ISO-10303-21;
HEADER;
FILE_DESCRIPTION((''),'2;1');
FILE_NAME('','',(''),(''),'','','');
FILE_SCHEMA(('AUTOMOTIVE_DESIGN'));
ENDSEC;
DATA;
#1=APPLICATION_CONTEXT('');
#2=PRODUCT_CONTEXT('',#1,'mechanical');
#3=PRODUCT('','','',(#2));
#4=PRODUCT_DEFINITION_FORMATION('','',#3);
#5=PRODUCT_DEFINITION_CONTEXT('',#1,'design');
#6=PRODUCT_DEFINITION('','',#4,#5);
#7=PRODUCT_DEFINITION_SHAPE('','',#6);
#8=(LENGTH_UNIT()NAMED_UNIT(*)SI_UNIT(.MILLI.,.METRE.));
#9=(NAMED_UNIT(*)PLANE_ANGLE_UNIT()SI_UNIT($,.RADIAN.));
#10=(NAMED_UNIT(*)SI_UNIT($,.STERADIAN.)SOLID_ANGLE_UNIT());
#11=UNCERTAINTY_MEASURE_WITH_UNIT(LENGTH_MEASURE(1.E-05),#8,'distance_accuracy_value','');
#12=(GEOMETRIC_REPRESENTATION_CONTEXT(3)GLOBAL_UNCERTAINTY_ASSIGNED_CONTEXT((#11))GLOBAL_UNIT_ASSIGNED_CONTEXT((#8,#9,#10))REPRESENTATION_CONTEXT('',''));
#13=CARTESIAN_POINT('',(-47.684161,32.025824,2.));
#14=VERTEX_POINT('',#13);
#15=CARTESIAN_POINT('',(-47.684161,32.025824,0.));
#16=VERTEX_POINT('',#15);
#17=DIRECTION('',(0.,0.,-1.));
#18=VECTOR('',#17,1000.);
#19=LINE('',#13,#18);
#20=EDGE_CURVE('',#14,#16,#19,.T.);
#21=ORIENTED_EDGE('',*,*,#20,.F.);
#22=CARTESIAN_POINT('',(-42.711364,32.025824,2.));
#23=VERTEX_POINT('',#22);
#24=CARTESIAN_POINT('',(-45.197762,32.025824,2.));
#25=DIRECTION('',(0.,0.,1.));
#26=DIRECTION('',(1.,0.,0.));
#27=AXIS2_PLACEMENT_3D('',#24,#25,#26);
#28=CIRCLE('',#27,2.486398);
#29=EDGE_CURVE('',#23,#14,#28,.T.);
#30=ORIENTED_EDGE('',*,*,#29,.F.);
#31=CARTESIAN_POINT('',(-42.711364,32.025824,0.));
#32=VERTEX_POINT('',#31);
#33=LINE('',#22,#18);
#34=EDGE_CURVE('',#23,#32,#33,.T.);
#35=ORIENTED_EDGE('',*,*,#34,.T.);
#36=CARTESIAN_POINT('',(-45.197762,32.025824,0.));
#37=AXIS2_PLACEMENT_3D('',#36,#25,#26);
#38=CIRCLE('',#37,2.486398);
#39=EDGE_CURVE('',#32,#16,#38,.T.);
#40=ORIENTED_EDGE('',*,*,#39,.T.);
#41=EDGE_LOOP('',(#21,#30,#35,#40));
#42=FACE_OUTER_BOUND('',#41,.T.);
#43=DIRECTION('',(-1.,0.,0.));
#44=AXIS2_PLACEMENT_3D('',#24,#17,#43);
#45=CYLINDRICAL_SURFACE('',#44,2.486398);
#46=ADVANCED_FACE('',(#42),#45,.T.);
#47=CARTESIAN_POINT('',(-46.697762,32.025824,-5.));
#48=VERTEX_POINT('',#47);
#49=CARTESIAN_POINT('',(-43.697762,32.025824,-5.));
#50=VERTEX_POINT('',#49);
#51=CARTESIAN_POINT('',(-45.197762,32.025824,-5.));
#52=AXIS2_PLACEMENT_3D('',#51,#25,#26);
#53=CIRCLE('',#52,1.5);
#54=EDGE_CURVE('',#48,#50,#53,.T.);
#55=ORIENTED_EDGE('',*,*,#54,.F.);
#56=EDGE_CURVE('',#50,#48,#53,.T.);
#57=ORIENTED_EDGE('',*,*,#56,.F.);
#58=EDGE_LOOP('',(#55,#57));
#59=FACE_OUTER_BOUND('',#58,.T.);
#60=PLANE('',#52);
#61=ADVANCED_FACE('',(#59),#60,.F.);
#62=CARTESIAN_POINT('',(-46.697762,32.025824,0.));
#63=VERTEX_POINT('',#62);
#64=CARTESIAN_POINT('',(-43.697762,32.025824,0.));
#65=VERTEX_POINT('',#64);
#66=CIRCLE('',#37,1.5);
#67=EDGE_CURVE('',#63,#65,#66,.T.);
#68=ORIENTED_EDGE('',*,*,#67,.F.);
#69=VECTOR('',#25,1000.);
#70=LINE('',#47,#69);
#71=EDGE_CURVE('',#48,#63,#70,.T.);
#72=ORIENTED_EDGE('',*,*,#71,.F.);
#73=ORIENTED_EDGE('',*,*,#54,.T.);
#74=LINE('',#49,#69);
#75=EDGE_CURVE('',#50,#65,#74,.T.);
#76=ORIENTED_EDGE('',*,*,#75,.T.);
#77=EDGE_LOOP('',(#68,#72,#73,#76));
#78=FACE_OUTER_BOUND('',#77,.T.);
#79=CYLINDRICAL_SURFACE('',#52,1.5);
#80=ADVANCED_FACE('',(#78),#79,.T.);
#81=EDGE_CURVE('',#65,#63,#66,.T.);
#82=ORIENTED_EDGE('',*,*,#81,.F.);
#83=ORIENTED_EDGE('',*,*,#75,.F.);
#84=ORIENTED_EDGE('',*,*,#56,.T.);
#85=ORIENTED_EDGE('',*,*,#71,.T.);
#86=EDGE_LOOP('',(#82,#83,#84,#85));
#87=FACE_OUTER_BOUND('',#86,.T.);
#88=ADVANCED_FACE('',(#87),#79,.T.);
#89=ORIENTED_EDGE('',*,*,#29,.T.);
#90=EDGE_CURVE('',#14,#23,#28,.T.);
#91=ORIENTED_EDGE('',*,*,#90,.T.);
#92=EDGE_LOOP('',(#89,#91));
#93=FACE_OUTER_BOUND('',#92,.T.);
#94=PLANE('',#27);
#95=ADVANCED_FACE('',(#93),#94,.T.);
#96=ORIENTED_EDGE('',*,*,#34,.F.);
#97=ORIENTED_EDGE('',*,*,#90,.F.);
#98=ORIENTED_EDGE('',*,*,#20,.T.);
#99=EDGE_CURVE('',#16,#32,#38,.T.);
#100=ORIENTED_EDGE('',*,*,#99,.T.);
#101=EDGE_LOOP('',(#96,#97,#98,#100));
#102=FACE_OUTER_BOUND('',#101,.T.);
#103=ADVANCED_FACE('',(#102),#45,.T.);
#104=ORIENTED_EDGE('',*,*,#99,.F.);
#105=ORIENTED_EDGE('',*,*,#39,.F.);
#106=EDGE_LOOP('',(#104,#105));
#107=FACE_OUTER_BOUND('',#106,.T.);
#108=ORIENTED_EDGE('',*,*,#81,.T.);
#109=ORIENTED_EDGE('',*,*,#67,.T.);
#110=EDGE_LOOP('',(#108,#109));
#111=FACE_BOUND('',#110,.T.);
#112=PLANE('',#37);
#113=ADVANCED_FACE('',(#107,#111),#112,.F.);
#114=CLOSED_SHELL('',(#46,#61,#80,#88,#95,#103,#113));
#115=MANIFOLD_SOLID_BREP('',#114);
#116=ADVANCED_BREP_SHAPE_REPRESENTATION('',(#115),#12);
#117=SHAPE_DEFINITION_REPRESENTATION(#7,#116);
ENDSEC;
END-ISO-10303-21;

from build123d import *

# Parameters (mm, degrees)
SKETCH1_R           = 1.5
BOSS_EXTRUDE1_DEPTH = 5
SKETCH2_R           = 2.486398422
BOSS_EXTRUDE2_DEPTH = 2


with BuildPart() as part:
    # Sketch1 → Boss-Extrude1 (new body)
    with BuildSketch(Plane.XY):
        with Locations((-45.197762361, 32.025823543)):
            Circle(SKETCH1_R)
    extrude(amount=-BOSS_EXTRUDE1_DEPTH)

    # Sketch2 → Boss-Extrude2 (add)
    with BuildSketch(Plane.XY):
        with Locations((-45.197762361, 32.025823543)):
            Circle(SKETCH2_R)
    extrude(amount=BOSS_EXTRUDE2_DEPTH)


solid = part.part
